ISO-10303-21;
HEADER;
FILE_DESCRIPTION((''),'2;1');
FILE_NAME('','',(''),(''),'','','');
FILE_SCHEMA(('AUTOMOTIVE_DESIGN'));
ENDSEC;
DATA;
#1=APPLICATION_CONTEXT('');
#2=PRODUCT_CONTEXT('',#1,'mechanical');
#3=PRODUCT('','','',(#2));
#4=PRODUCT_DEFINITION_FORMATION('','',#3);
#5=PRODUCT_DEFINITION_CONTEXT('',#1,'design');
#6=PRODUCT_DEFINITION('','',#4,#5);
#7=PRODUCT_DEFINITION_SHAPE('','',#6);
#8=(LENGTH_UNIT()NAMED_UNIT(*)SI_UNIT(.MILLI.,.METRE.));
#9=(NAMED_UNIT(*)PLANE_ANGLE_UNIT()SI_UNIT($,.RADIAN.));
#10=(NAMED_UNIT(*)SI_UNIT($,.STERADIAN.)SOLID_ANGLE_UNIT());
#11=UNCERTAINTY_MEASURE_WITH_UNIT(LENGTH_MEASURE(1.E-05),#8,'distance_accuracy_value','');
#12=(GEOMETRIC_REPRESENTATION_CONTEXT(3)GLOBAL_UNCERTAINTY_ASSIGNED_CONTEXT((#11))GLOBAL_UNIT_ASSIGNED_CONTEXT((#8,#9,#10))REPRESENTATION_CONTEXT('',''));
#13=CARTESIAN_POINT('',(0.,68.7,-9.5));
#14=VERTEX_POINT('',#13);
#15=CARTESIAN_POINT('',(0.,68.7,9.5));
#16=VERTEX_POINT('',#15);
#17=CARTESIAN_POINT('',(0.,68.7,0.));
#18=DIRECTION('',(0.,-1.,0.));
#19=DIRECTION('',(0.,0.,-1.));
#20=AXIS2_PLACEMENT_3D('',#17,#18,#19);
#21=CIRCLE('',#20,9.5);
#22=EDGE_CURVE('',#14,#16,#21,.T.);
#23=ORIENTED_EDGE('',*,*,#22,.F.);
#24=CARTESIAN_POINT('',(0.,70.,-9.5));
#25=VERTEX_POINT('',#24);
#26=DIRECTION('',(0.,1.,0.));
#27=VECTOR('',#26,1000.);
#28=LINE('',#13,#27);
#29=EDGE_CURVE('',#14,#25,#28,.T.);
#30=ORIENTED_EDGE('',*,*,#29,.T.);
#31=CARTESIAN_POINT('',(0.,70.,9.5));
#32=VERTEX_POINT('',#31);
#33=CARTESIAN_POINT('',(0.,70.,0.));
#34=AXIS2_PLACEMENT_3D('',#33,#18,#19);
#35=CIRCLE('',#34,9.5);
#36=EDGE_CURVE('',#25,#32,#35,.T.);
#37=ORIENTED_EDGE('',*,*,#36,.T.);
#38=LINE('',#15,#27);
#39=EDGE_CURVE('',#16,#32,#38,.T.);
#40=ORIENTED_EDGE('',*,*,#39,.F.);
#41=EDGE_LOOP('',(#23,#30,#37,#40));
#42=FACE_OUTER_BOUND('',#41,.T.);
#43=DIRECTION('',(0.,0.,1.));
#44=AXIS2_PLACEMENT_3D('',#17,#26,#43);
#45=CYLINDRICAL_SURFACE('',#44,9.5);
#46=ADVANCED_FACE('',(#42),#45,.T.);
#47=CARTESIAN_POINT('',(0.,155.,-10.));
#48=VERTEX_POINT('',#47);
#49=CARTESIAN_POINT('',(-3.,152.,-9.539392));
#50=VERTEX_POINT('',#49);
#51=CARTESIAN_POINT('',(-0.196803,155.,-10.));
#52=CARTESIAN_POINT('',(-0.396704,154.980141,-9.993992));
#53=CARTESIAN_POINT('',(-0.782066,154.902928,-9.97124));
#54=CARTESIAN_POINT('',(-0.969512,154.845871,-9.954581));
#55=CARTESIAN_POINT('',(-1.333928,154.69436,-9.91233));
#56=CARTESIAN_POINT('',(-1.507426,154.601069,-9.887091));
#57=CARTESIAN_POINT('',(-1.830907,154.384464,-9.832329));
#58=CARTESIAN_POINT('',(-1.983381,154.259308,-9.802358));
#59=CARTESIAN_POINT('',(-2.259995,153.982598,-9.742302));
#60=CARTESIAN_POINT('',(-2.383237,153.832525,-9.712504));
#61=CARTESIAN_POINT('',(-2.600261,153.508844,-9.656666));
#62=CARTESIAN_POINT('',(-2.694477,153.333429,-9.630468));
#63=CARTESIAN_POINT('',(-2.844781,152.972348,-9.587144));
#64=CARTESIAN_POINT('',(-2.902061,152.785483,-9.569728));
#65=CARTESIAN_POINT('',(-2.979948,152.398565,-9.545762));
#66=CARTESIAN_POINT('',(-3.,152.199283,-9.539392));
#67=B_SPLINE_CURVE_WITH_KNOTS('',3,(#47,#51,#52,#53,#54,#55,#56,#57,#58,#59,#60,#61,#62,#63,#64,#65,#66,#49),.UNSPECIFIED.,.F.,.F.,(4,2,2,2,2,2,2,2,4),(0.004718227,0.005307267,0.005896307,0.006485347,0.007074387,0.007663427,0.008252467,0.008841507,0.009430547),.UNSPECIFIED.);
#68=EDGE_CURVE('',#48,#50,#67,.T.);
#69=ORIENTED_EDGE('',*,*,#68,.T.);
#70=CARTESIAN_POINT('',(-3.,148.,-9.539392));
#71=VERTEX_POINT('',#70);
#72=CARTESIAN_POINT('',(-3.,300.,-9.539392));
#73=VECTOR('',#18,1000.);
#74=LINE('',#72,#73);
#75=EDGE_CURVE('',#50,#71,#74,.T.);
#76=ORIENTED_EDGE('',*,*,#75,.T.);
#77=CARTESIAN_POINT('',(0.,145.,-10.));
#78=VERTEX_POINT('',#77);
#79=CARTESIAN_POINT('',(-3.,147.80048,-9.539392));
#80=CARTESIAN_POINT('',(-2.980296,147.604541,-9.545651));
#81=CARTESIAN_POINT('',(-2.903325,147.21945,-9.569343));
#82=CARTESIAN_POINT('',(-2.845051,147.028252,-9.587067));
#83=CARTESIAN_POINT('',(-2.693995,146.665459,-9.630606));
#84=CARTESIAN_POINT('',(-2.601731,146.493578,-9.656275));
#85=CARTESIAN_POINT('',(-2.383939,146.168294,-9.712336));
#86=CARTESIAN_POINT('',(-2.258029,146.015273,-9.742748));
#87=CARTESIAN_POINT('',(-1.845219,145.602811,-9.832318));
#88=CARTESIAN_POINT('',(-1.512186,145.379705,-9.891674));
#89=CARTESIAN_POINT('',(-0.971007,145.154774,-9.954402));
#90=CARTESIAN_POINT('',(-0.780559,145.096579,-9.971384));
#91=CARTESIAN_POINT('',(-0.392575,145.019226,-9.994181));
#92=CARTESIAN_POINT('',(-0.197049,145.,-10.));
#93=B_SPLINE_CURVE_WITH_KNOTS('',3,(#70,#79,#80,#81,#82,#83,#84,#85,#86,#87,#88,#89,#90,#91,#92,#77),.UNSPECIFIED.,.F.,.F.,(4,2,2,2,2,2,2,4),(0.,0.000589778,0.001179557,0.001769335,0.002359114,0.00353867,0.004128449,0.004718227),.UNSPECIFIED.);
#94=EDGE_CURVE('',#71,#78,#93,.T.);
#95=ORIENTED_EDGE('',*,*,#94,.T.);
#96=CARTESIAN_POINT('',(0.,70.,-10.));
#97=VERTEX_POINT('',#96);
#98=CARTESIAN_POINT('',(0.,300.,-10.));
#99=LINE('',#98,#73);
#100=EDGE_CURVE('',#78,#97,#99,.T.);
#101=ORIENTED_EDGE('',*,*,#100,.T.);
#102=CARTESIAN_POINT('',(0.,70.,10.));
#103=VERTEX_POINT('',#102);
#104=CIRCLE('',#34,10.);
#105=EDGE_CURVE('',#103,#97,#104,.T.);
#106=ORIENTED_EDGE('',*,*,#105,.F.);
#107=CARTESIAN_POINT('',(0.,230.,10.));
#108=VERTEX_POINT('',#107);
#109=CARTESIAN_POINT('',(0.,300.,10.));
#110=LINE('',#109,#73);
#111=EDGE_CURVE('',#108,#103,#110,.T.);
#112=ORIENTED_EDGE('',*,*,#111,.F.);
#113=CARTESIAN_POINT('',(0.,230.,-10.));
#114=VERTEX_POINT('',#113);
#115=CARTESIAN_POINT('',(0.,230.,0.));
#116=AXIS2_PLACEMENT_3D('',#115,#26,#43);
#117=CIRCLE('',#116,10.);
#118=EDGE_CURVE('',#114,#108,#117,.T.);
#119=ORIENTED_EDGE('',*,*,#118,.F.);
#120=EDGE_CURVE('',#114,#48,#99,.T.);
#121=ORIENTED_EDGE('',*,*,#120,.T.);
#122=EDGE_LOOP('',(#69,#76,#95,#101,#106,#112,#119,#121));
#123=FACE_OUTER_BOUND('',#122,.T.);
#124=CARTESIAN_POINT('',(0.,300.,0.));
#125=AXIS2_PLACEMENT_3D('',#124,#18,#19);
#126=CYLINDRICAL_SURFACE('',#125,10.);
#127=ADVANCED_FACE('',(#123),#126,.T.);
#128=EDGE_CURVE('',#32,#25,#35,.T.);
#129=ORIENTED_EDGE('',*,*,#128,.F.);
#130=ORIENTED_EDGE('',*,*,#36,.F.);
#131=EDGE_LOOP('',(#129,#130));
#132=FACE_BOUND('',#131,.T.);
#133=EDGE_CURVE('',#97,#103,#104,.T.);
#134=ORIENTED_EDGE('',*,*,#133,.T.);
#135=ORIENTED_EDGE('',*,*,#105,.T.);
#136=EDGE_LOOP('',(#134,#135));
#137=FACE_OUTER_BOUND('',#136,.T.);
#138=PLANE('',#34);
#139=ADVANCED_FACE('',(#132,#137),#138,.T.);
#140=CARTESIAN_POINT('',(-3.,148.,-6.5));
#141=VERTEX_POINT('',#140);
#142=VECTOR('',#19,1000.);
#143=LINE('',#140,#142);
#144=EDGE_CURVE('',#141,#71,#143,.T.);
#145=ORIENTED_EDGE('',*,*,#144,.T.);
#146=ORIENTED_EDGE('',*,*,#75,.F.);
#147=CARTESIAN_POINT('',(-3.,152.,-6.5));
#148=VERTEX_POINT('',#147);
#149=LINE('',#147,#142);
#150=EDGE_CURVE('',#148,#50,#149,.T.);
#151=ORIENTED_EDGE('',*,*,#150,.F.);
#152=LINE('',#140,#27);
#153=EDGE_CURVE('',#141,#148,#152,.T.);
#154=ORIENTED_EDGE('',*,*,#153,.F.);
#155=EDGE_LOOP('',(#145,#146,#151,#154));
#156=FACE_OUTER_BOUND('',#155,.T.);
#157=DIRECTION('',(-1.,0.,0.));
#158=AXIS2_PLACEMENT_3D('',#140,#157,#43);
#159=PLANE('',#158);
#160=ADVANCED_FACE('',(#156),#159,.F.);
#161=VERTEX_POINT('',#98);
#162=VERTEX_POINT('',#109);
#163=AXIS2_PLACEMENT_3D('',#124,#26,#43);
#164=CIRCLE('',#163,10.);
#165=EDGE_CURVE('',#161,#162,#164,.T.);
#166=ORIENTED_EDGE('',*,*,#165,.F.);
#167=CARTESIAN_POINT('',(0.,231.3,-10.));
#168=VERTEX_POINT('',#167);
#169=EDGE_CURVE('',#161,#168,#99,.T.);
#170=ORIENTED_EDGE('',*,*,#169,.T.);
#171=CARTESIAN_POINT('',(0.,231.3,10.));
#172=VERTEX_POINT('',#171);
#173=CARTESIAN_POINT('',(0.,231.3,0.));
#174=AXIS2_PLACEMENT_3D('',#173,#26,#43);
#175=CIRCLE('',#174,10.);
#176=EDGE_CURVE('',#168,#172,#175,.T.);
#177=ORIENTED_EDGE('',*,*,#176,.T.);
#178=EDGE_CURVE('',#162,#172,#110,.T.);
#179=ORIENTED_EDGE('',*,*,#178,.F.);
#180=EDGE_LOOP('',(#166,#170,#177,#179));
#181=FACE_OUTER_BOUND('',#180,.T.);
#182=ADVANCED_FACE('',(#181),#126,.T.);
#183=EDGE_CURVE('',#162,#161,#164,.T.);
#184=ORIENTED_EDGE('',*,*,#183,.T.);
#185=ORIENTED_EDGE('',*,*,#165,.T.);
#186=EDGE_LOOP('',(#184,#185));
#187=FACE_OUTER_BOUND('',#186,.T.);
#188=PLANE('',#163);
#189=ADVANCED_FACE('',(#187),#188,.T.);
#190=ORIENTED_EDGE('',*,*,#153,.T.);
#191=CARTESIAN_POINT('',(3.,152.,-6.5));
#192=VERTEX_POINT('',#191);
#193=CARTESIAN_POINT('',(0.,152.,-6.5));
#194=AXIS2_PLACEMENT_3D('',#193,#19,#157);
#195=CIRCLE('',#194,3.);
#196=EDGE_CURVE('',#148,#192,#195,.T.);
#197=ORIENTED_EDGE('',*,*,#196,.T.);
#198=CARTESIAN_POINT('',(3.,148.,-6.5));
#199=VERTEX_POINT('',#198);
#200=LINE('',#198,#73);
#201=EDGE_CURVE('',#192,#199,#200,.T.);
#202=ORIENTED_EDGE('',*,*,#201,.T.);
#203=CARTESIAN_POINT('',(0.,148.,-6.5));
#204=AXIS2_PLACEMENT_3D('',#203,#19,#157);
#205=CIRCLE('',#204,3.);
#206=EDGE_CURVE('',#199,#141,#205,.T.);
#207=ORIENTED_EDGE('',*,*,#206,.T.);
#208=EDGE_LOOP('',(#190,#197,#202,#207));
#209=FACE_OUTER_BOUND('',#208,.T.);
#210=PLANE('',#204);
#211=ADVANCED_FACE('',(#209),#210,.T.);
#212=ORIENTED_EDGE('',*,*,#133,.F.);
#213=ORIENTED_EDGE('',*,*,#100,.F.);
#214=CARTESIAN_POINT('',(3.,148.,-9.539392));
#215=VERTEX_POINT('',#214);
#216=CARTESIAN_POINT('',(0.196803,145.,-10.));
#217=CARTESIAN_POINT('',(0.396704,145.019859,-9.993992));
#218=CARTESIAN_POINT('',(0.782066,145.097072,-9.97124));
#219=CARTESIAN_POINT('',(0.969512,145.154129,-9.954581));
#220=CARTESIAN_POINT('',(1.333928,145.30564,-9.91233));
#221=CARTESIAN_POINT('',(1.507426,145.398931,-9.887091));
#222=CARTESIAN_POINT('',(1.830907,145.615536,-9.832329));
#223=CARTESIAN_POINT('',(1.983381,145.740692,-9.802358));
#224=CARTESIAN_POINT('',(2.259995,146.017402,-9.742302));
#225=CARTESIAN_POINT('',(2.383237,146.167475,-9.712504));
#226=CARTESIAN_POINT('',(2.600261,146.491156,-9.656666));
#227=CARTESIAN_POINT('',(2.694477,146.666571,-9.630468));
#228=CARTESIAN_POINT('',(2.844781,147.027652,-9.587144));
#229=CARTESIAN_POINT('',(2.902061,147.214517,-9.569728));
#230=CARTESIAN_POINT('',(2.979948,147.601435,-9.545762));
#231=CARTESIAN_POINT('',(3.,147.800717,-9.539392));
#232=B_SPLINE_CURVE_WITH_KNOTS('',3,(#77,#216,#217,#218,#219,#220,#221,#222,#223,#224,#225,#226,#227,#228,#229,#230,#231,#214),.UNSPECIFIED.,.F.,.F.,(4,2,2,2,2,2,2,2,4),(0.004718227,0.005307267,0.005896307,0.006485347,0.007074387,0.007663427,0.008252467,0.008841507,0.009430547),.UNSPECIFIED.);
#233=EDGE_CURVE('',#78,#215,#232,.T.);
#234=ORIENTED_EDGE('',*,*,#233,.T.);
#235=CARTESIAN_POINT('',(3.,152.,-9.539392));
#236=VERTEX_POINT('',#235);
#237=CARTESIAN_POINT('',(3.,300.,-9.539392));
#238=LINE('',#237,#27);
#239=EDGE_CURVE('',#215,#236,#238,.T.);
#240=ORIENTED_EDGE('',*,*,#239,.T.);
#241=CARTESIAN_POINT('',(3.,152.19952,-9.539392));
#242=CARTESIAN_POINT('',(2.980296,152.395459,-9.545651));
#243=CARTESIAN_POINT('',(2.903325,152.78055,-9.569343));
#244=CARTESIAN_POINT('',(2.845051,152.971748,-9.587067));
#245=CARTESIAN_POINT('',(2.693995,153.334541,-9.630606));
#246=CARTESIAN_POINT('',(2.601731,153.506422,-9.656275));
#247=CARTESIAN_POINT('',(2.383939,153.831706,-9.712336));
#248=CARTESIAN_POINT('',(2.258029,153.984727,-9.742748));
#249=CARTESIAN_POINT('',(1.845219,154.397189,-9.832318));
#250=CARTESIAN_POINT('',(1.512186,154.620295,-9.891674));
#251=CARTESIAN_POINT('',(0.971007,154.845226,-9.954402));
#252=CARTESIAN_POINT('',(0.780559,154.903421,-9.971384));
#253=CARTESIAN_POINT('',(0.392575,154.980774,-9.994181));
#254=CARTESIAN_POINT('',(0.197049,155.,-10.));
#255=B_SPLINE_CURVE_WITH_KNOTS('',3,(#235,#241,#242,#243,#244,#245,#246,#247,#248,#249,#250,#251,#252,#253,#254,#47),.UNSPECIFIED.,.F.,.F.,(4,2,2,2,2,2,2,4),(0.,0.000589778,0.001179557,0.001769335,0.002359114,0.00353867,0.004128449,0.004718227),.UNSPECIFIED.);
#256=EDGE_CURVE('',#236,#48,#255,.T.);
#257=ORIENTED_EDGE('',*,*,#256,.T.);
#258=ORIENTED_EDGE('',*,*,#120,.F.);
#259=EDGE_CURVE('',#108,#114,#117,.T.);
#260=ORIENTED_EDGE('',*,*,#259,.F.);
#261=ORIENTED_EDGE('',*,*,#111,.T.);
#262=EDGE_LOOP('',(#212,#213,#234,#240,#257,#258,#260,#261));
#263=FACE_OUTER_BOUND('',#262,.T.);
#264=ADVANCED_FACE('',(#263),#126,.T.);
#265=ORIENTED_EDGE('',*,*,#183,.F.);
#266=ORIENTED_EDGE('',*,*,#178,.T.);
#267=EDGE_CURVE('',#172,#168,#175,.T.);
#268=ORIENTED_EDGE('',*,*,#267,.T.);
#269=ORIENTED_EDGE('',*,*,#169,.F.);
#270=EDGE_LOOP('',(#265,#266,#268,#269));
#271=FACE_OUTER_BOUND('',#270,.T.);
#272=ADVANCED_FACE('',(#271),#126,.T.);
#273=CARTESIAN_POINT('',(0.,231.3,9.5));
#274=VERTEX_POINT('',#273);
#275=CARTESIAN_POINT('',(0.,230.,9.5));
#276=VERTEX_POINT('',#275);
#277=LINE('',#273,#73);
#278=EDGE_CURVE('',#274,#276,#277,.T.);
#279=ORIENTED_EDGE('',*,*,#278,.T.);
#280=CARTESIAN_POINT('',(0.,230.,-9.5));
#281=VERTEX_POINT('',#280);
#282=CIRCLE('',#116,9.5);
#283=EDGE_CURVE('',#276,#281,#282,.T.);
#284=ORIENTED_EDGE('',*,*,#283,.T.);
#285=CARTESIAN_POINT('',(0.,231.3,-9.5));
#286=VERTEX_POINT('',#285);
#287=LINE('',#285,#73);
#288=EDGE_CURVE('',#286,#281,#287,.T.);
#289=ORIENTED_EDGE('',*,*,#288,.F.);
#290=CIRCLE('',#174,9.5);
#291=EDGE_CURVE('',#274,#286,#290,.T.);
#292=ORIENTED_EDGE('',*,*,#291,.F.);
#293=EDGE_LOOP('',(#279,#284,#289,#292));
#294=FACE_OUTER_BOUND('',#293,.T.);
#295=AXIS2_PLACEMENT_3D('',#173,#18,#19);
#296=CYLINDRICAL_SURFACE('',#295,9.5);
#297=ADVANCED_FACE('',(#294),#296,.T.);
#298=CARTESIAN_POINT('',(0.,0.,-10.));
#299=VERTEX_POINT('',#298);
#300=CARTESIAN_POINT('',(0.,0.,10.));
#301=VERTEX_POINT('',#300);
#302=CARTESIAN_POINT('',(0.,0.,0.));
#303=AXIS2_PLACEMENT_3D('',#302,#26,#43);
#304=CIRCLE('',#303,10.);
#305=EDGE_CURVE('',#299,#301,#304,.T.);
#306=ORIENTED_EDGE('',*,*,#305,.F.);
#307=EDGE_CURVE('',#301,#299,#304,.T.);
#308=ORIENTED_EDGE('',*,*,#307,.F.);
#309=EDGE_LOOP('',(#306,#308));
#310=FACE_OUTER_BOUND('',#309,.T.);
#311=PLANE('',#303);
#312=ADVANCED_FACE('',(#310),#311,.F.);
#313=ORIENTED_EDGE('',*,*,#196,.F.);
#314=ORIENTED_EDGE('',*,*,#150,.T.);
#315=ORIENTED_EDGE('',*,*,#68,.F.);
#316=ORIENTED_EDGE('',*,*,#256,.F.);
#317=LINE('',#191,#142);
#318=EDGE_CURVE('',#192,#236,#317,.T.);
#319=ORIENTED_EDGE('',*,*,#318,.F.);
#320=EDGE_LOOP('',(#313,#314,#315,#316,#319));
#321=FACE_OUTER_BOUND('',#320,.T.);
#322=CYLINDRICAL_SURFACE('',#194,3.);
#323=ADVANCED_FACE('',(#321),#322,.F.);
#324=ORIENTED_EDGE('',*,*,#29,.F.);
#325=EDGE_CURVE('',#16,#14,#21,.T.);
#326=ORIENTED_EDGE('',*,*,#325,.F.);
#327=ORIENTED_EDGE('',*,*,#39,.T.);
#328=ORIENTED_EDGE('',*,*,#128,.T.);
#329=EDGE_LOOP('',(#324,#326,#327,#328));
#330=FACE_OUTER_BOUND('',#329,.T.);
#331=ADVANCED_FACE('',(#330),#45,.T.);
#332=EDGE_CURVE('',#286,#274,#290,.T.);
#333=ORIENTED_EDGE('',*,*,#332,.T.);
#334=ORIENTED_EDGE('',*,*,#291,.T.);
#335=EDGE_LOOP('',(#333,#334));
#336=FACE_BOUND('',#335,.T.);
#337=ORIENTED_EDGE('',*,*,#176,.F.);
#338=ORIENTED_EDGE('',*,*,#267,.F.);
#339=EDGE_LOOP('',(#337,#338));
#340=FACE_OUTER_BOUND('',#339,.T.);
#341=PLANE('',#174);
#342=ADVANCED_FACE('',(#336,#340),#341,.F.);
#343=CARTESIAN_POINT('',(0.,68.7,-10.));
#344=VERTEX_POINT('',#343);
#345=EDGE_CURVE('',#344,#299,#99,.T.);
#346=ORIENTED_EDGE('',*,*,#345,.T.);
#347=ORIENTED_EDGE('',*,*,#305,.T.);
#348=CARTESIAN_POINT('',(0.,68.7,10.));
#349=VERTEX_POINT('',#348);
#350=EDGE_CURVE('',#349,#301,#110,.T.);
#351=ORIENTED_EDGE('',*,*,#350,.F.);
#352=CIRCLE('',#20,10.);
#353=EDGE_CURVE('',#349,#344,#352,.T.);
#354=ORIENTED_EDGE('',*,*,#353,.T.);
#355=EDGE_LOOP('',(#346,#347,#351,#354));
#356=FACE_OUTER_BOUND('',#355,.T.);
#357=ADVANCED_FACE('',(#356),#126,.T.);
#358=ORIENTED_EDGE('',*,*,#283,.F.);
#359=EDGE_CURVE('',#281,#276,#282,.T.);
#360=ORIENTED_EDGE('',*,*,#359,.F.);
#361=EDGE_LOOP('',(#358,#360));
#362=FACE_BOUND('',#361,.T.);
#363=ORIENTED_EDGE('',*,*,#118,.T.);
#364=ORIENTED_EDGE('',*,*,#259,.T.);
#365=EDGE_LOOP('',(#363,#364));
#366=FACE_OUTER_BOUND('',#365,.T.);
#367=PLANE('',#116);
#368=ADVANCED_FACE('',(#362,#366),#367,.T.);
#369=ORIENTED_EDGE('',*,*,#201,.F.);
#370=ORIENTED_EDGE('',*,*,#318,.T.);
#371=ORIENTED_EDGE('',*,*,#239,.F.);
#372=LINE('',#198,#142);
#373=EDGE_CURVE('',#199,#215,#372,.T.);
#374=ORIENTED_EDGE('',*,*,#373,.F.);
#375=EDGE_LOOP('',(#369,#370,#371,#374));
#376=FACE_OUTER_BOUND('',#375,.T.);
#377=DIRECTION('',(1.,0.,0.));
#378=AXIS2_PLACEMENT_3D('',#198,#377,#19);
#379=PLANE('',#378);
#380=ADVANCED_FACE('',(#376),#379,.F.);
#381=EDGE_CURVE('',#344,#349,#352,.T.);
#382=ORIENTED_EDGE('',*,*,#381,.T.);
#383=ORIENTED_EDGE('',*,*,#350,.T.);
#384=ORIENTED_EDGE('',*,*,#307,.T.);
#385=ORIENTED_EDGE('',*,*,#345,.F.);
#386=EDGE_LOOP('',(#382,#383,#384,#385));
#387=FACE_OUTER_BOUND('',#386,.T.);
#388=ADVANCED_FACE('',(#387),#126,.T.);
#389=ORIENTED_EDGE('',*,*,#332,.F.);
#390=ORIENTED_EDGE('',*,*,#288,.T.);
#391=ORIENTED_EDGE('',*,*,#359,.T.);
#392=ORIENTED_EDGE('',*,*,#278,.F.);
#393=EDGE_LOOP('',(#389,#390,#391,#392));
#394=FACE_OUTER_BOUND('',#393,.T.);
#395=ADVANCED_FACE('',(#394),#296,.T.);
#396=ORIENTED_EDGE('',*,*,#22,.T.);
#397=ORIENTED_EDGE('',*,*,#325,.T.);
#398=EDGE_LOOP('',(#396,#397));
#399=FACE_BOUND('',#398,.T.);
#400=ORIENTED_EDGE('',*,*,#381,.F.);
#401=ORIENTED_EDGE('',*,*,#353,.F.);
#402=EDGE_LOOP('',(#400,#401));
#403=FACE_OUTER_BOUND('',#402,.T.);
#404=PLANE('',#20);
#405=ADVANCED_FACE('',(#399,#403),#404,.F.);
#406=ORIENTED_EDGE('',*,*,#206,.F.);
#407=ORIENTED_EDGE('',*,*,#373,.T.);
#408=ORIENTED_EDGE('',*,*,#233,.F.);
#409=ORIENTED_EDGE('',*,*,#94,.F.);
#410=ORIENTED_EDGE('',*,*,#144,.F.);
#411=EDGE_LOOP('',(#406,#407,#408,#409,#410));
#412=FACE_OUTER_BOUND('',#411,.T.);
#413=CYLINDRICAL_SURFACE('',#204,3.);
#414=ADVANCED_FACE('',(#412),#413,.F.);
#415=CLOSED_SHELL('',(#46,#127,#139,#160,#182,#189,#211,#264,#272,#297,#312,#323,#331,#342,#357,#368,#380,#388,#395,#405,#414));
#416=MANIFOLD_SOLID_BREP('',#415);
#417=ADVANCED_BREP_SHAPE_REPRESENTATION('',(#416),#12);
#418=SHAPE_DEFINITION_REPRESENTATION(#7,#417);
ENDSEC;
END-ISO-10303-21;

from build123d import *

# Parameters (mm, degrees)
SKETCH_1_R          = 10
EXTRUDE_1_DEPTH     = 300
CUT_EXTRUDE_START   = 1.3
SKETCH_7_R          = 10
SKETCH_7_R_2        = 9.5
CUT_EXTRUDE_3_DEPTH = 1.3
SKETCH_8_R          = 10
SKETCH_8_R_2        = 9.5
CUT_EXTRUDE_4_DEPTH = 1.3
ZJCQC_DEPTH         = 3.5


with BuildPart() as part:
    # 草图1 → 凸台-拉伸1 (new body)
    with BuildSketch(Plane(origin=(0, 0, 0), x_dir=(1, 0, 0), z_dir=(0, 1, 0))):
        with Locations(Location((0, 0, 0), (0, 0, 270))):
            Circle(SKETCH_1_R)
    extrude(amount=EXTRUDE_1_DEPTH)

    # 草图7 → 切除-拉伸3 (cut)
    with BuildSketch(Plane(origin=(0, 70, 0), x_dir=(-1, 0, 0), z_dir=(0, -1, 0)).offset(CUT_EXTRUDE_START)):
        with Locations(Location((0, 0, 0), (0, 0, 90))):
            Circle(SKETCH_7_R)
        with Locations(Location((0, 0, 0), (0, 0, 90))):
            Circle(SKETCH_7_R_2, mode=Mode.SUBTRACT)
    extrude(amount=-CUT_EXTRUDE_3_DEPTH, mode=Mode.SUBTRACT)

    # 草图8 → 切除-拉伸4 (cut)
    with BuildSketch(Plane(origin=(0, 230, 0), x_dir=(1, 0, 0), z_dir=(0, 1, 0))):
        with Locations(Location((0, 0, 0), (0, 0, 90))):
            Circle(SKETCH_8_R)
        with Locations(Location((0, 0, 0), (0, 0, 90))):
            Circle(SKETCH_8_R_2, mode=Mode.SUBTRACT)
    extrude(amount=CUT_EXTRUDE_4_DEPTH, mode=Mode.SUBTRACT)

    # MyToolsZJC → ZJCQC (cut)
    with BuildSketch(Plane.YX.offset(10)):
        with BuildLine():
            Line((148, 3), (152, 3))
            ThreePointArc((152, 3), (155, 0), (152, -3))
            Line((152, -3), (148, -3))
            ThreePointArc((148, -3), (145, 0), (148, 3))
        make_face()
    extrude(amount=-ZJCQC_DEPTH, mode=Mode.SUBTRACT)


solid = part.part
